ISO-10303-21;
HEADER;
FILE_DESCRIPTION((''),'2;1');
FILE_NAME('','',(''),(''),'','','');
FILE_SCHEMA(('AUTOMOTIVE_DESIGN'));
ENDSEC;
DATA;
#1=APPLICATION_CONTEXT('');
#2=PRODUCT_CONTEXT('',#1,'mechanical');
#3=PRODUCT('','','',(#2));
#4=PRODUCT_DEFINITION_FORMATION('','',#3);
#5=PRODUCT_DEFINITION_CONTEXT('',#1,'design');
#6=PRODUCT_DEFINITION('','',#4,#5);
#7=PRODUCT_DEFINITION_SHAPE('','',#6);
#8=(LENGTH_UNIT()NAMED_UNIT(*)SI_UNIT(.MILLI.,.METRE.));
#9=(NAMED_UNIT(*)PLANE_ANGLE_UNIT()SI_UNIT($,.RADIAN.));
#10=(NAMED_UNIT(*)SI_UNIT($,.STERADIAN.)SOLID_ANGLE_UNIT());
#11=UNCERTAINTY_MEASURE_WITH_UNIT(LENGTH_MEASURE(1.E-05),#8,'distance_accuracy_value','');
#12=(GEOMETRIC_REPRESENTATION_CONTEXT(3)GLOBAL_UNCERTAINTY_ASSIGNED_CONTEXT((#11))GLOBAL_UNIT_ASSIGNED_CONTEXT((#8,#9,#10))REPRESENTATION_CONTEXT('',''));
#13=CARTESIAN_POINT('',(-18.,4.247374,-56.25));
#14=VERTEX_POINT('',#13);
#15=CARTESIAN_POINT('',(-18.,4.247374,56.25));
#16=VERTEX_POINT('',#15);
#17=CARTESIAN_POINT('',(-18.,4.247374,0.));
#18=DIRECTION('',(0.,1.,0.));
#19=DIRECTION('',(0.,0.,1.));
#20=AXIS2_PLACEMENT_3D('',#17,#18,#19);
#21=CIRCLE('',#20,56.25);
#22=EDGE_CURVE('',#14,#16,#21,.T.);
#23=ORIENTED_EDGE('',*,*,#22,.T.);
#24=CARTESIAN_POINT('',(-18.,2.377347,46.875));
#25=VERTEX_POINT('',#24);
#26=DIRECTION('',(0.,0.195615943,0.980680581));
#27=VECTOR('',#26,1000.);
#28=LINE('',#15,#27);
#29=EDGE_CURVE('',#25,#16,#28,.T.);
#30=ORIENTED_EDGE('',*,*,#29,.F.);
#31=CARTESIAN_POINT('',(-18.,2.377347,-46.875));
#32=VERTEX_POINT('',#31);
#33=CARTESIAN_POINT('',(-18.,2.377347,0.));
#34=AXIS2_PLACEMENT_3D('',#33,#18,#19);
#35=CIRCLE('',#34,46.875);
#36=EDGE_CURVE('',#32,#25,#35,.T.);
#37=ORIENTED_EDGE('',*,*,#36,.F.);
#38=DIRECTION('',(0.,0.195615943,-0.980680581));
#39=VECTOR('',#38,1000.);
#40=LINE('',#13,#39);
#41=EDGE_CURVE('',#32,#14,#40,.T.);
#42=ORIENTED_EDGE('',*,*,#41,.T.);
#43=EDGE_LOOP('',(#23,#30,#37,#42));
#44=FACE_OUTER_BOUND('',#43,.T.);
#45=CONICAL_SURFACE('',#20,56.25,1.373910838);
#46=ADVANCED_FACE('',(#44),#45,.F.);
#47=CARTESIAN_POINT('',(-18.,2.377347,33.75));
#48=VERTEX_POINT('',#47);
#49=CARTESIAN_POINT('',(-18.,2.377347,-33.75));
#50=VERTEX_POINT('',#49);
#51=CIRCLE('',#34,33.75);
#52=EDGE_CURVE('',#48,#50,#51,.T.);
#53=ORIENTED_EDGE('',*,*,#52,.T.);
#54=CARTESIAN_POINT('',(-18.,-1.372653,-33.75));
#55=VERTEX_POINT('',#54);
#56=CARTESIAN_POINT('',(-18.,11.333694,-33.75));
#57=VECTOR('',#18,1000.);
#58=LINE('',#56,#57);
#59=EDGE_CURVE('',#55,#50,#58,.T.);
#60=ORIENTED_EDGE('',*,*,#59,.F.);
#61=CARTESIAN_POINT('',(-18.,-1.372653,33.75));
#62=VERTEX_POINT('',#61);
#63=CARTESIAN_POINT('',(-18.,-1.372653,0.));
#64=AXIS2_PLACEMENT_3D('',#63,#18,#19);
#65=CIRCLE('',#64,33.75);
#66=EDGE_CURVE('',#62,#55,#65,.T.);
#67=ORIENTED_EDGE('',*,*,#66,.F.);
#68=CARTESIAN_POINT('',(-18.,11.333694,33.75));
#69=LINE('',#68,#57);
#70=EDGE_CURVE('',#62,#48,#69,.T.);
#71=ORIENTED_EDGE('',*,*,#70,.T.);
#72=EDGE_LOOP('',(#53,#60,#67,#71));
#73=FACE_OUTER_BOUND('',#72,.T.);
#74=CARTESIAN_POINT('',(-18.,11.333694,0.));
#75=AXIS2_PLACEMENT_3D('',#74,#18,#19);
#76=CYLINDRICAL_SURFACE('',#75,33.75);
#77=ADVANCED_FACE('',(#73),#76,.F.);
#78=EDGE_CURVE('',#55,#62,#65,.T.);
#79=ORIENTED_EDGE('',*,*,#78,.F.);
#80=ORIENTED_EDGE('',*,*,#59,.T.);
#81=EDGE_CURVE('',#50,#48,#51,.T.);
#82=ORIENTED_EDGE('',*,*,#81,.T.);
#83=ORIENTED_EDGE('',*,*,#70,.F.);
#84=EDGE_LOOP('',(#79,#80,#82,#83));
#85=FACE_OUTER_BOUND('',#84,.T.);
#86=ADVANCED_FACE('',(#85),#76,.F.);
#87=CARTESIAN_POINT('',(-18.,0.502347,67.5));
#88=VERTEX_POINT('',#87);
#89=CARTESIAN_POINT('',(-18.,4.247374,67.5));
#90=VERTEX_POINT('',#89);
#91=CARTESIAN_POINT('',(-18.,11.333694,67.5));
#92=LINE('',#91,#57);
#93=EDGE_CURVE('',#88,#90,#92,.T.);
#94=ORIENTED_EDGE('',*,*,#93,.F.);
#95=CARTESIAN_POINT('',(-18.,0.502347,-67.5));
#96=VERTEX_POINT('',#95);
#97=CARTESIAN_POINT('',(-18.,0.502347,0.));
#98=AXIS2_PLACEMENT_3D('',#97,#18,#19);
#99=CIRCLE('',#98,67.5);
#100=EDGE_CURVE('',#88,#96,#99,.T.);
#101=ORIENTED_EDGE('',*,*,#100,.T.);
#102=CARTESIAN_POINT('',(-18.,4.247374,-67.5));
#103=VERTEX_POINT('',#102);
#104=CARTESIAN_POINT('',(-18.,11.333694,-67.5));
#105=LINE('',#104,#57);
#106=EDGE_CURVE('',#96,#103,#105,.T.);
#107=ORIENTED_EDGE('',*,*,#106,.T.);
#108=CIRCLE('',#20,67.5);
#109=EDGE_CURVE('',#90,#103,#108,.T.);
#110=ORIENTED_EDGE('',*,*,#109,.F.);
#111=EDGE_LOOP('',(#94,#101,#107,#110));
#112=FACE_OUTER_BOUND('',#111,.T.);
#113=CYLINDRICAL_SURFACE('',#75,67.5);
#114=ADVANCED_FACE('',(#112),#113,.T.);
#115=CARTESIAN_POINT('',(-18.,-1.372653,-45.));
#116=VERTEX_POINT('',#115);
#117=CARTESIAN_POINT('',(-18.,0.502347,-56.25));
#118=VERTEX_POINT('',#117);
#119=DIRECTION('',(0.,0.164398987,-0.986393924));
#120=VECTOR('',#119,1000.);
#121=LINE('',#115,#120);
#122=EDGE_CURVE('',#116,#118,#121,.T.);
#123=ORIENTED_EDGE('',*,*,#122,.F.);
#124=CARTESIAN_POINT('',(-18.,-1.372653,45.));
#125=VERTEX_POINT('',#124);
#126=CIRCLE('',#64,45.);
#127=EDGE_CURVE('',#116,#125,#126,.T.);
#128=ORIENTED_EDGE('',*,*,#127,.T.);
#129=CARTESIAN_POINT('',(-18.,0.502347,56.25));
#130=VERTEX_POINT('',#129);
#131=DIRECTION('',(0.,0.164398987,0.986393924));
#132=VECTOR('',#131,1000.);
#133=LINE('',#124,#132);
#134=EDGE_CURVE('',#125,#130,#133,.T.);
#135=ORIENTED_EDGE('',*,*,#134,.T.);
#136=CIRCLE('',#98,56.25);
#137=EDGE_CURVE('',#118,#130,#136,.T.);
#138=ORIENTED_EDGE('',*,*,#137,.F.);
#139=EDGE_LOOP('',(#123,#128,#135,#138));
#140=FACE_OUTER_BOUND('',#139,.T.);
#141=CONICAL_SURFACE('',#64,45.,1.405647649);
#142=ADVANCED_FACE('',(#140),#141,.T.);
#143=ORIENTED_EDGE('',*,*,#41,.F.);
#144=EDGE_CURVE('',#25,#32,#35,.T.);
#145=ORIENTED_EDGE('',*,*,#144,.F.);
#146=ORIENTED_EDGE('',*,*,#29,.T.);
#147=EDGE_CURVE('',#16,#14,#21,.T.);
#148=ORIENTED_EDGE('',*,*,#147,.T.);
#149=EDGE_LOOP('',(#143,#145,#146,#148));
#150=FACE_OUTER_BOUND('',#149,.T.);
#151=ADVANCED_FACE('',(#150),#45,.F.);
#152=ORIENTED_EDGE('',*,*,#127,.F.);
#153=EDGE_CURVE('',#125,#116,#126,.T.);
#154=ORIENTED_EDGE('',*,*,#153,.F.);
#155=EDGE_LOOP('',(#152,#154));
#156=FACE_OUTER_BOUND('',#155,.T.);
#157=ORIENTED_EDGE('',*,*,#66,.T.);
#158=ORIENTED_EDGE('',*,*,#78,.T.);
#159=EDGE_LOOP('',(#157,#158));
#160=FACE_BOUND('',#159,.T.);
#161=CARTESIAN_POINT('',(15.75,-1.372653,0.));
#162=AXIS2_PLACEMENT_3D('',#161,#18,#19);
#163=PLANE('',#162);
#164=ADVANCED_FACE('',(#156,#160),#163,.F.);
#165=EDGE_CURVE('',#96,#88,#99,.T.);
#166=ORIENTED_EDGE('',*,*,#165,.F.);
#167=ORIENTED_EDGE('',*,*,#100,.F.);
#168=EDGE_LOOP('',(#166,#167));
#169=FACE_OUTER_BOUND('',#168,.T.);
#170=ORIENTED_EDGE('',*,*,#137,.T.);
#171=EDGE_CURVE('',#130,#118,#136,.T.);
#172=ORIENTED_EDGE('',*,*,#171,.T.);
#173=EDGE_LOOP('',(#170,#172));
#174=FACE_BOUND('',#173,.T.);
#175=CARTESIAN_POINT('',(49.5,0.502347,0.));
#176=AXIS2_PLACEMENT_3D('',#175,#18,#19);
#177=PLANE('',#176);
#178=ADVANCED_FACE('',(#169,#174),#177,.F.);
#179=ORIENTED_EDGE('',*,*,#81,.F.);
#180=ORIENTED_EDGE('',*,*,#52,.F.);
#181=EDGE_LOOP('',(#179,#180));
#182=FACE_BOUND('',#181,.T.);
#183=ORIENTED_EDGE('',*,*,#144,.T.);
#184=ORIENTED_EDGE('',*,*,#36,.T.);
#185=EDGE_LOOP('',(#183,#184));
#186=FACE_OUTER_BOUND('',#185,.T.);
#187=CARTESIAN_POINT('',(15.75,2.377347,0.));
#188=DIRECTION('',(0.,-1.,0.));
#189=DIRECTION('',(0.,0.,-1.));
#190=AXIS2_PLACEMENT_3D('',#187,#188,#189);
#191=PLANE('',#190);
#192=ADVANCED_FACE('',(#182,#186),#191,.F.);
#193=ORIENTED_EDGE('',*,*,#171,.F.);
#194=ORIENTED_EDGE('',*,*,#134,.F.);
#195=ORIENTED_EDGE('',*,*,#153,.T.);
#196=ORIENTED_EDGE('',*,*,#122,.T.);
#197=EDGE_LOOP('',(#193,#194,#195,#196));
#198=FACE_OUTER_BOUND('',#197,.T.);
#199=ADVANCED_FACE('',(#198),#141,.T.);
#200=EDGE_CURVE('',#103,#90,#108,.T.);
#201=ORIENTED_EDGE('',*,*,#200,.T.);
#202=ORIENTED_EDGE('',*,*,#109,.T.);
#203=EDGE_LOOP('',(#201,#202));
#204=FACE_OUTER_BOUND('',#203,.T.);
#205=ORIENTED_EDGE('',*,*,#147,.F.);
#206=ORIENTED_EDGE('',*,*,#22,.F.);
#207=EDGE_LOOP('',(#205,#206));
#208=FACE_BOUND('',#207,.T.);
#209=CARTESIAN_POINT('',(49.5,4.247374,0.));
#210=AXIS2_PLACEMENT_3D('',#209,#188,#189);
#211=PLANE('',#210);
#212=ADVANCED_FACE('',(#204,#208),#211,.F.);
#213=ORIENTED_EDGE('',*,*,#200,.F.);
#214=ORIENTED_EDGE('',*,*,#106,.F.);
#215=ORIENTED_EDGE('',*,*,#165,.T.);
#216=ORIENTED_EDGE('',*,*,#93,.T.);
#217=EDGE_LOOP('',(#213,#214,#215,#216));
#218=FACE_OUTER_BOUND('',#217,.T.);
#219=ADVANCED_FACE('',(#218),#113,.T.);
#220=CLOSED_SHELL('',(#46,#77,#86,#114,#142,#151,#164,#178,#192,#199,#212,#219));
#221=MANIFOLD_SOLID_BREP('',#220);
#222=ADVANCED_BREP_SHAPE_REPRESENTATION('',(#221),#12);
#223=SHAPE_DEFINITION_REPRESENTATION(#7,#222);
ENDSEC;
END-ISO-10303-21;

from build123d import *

# Parameters (mm, degrees)
SCALE_1_SCALE = 1.875


with BuildPart() as part:
    # Sketch1 → Revolve1 (revolve)
    with BuildSketch(Plane.XY, mode=Mode.PRIVATE) as revolve1_sk:
        Polygon((0, 0), (0, 2), (7, 2), (12, 2.997347898), (18, 2.997347898), (18, 1), (12, 1), (6, 0), align=None)
    revolve(revolve1_sk.sketch.rotate(Axis((-18, 6.77671814, 0), (0, -1, 0)), 90), axis=Axis((-18, 6.77671814, 0), (0, -1, 0)))


with BuildPart() as part_1:
    # Scale 1: scaled about (-18, 1.56874625, 0)
    add(part.part.scale(SCALE_1_SCALE).moved(Location((15.75, -1.372652969, 0))))


solid = part_1.part
